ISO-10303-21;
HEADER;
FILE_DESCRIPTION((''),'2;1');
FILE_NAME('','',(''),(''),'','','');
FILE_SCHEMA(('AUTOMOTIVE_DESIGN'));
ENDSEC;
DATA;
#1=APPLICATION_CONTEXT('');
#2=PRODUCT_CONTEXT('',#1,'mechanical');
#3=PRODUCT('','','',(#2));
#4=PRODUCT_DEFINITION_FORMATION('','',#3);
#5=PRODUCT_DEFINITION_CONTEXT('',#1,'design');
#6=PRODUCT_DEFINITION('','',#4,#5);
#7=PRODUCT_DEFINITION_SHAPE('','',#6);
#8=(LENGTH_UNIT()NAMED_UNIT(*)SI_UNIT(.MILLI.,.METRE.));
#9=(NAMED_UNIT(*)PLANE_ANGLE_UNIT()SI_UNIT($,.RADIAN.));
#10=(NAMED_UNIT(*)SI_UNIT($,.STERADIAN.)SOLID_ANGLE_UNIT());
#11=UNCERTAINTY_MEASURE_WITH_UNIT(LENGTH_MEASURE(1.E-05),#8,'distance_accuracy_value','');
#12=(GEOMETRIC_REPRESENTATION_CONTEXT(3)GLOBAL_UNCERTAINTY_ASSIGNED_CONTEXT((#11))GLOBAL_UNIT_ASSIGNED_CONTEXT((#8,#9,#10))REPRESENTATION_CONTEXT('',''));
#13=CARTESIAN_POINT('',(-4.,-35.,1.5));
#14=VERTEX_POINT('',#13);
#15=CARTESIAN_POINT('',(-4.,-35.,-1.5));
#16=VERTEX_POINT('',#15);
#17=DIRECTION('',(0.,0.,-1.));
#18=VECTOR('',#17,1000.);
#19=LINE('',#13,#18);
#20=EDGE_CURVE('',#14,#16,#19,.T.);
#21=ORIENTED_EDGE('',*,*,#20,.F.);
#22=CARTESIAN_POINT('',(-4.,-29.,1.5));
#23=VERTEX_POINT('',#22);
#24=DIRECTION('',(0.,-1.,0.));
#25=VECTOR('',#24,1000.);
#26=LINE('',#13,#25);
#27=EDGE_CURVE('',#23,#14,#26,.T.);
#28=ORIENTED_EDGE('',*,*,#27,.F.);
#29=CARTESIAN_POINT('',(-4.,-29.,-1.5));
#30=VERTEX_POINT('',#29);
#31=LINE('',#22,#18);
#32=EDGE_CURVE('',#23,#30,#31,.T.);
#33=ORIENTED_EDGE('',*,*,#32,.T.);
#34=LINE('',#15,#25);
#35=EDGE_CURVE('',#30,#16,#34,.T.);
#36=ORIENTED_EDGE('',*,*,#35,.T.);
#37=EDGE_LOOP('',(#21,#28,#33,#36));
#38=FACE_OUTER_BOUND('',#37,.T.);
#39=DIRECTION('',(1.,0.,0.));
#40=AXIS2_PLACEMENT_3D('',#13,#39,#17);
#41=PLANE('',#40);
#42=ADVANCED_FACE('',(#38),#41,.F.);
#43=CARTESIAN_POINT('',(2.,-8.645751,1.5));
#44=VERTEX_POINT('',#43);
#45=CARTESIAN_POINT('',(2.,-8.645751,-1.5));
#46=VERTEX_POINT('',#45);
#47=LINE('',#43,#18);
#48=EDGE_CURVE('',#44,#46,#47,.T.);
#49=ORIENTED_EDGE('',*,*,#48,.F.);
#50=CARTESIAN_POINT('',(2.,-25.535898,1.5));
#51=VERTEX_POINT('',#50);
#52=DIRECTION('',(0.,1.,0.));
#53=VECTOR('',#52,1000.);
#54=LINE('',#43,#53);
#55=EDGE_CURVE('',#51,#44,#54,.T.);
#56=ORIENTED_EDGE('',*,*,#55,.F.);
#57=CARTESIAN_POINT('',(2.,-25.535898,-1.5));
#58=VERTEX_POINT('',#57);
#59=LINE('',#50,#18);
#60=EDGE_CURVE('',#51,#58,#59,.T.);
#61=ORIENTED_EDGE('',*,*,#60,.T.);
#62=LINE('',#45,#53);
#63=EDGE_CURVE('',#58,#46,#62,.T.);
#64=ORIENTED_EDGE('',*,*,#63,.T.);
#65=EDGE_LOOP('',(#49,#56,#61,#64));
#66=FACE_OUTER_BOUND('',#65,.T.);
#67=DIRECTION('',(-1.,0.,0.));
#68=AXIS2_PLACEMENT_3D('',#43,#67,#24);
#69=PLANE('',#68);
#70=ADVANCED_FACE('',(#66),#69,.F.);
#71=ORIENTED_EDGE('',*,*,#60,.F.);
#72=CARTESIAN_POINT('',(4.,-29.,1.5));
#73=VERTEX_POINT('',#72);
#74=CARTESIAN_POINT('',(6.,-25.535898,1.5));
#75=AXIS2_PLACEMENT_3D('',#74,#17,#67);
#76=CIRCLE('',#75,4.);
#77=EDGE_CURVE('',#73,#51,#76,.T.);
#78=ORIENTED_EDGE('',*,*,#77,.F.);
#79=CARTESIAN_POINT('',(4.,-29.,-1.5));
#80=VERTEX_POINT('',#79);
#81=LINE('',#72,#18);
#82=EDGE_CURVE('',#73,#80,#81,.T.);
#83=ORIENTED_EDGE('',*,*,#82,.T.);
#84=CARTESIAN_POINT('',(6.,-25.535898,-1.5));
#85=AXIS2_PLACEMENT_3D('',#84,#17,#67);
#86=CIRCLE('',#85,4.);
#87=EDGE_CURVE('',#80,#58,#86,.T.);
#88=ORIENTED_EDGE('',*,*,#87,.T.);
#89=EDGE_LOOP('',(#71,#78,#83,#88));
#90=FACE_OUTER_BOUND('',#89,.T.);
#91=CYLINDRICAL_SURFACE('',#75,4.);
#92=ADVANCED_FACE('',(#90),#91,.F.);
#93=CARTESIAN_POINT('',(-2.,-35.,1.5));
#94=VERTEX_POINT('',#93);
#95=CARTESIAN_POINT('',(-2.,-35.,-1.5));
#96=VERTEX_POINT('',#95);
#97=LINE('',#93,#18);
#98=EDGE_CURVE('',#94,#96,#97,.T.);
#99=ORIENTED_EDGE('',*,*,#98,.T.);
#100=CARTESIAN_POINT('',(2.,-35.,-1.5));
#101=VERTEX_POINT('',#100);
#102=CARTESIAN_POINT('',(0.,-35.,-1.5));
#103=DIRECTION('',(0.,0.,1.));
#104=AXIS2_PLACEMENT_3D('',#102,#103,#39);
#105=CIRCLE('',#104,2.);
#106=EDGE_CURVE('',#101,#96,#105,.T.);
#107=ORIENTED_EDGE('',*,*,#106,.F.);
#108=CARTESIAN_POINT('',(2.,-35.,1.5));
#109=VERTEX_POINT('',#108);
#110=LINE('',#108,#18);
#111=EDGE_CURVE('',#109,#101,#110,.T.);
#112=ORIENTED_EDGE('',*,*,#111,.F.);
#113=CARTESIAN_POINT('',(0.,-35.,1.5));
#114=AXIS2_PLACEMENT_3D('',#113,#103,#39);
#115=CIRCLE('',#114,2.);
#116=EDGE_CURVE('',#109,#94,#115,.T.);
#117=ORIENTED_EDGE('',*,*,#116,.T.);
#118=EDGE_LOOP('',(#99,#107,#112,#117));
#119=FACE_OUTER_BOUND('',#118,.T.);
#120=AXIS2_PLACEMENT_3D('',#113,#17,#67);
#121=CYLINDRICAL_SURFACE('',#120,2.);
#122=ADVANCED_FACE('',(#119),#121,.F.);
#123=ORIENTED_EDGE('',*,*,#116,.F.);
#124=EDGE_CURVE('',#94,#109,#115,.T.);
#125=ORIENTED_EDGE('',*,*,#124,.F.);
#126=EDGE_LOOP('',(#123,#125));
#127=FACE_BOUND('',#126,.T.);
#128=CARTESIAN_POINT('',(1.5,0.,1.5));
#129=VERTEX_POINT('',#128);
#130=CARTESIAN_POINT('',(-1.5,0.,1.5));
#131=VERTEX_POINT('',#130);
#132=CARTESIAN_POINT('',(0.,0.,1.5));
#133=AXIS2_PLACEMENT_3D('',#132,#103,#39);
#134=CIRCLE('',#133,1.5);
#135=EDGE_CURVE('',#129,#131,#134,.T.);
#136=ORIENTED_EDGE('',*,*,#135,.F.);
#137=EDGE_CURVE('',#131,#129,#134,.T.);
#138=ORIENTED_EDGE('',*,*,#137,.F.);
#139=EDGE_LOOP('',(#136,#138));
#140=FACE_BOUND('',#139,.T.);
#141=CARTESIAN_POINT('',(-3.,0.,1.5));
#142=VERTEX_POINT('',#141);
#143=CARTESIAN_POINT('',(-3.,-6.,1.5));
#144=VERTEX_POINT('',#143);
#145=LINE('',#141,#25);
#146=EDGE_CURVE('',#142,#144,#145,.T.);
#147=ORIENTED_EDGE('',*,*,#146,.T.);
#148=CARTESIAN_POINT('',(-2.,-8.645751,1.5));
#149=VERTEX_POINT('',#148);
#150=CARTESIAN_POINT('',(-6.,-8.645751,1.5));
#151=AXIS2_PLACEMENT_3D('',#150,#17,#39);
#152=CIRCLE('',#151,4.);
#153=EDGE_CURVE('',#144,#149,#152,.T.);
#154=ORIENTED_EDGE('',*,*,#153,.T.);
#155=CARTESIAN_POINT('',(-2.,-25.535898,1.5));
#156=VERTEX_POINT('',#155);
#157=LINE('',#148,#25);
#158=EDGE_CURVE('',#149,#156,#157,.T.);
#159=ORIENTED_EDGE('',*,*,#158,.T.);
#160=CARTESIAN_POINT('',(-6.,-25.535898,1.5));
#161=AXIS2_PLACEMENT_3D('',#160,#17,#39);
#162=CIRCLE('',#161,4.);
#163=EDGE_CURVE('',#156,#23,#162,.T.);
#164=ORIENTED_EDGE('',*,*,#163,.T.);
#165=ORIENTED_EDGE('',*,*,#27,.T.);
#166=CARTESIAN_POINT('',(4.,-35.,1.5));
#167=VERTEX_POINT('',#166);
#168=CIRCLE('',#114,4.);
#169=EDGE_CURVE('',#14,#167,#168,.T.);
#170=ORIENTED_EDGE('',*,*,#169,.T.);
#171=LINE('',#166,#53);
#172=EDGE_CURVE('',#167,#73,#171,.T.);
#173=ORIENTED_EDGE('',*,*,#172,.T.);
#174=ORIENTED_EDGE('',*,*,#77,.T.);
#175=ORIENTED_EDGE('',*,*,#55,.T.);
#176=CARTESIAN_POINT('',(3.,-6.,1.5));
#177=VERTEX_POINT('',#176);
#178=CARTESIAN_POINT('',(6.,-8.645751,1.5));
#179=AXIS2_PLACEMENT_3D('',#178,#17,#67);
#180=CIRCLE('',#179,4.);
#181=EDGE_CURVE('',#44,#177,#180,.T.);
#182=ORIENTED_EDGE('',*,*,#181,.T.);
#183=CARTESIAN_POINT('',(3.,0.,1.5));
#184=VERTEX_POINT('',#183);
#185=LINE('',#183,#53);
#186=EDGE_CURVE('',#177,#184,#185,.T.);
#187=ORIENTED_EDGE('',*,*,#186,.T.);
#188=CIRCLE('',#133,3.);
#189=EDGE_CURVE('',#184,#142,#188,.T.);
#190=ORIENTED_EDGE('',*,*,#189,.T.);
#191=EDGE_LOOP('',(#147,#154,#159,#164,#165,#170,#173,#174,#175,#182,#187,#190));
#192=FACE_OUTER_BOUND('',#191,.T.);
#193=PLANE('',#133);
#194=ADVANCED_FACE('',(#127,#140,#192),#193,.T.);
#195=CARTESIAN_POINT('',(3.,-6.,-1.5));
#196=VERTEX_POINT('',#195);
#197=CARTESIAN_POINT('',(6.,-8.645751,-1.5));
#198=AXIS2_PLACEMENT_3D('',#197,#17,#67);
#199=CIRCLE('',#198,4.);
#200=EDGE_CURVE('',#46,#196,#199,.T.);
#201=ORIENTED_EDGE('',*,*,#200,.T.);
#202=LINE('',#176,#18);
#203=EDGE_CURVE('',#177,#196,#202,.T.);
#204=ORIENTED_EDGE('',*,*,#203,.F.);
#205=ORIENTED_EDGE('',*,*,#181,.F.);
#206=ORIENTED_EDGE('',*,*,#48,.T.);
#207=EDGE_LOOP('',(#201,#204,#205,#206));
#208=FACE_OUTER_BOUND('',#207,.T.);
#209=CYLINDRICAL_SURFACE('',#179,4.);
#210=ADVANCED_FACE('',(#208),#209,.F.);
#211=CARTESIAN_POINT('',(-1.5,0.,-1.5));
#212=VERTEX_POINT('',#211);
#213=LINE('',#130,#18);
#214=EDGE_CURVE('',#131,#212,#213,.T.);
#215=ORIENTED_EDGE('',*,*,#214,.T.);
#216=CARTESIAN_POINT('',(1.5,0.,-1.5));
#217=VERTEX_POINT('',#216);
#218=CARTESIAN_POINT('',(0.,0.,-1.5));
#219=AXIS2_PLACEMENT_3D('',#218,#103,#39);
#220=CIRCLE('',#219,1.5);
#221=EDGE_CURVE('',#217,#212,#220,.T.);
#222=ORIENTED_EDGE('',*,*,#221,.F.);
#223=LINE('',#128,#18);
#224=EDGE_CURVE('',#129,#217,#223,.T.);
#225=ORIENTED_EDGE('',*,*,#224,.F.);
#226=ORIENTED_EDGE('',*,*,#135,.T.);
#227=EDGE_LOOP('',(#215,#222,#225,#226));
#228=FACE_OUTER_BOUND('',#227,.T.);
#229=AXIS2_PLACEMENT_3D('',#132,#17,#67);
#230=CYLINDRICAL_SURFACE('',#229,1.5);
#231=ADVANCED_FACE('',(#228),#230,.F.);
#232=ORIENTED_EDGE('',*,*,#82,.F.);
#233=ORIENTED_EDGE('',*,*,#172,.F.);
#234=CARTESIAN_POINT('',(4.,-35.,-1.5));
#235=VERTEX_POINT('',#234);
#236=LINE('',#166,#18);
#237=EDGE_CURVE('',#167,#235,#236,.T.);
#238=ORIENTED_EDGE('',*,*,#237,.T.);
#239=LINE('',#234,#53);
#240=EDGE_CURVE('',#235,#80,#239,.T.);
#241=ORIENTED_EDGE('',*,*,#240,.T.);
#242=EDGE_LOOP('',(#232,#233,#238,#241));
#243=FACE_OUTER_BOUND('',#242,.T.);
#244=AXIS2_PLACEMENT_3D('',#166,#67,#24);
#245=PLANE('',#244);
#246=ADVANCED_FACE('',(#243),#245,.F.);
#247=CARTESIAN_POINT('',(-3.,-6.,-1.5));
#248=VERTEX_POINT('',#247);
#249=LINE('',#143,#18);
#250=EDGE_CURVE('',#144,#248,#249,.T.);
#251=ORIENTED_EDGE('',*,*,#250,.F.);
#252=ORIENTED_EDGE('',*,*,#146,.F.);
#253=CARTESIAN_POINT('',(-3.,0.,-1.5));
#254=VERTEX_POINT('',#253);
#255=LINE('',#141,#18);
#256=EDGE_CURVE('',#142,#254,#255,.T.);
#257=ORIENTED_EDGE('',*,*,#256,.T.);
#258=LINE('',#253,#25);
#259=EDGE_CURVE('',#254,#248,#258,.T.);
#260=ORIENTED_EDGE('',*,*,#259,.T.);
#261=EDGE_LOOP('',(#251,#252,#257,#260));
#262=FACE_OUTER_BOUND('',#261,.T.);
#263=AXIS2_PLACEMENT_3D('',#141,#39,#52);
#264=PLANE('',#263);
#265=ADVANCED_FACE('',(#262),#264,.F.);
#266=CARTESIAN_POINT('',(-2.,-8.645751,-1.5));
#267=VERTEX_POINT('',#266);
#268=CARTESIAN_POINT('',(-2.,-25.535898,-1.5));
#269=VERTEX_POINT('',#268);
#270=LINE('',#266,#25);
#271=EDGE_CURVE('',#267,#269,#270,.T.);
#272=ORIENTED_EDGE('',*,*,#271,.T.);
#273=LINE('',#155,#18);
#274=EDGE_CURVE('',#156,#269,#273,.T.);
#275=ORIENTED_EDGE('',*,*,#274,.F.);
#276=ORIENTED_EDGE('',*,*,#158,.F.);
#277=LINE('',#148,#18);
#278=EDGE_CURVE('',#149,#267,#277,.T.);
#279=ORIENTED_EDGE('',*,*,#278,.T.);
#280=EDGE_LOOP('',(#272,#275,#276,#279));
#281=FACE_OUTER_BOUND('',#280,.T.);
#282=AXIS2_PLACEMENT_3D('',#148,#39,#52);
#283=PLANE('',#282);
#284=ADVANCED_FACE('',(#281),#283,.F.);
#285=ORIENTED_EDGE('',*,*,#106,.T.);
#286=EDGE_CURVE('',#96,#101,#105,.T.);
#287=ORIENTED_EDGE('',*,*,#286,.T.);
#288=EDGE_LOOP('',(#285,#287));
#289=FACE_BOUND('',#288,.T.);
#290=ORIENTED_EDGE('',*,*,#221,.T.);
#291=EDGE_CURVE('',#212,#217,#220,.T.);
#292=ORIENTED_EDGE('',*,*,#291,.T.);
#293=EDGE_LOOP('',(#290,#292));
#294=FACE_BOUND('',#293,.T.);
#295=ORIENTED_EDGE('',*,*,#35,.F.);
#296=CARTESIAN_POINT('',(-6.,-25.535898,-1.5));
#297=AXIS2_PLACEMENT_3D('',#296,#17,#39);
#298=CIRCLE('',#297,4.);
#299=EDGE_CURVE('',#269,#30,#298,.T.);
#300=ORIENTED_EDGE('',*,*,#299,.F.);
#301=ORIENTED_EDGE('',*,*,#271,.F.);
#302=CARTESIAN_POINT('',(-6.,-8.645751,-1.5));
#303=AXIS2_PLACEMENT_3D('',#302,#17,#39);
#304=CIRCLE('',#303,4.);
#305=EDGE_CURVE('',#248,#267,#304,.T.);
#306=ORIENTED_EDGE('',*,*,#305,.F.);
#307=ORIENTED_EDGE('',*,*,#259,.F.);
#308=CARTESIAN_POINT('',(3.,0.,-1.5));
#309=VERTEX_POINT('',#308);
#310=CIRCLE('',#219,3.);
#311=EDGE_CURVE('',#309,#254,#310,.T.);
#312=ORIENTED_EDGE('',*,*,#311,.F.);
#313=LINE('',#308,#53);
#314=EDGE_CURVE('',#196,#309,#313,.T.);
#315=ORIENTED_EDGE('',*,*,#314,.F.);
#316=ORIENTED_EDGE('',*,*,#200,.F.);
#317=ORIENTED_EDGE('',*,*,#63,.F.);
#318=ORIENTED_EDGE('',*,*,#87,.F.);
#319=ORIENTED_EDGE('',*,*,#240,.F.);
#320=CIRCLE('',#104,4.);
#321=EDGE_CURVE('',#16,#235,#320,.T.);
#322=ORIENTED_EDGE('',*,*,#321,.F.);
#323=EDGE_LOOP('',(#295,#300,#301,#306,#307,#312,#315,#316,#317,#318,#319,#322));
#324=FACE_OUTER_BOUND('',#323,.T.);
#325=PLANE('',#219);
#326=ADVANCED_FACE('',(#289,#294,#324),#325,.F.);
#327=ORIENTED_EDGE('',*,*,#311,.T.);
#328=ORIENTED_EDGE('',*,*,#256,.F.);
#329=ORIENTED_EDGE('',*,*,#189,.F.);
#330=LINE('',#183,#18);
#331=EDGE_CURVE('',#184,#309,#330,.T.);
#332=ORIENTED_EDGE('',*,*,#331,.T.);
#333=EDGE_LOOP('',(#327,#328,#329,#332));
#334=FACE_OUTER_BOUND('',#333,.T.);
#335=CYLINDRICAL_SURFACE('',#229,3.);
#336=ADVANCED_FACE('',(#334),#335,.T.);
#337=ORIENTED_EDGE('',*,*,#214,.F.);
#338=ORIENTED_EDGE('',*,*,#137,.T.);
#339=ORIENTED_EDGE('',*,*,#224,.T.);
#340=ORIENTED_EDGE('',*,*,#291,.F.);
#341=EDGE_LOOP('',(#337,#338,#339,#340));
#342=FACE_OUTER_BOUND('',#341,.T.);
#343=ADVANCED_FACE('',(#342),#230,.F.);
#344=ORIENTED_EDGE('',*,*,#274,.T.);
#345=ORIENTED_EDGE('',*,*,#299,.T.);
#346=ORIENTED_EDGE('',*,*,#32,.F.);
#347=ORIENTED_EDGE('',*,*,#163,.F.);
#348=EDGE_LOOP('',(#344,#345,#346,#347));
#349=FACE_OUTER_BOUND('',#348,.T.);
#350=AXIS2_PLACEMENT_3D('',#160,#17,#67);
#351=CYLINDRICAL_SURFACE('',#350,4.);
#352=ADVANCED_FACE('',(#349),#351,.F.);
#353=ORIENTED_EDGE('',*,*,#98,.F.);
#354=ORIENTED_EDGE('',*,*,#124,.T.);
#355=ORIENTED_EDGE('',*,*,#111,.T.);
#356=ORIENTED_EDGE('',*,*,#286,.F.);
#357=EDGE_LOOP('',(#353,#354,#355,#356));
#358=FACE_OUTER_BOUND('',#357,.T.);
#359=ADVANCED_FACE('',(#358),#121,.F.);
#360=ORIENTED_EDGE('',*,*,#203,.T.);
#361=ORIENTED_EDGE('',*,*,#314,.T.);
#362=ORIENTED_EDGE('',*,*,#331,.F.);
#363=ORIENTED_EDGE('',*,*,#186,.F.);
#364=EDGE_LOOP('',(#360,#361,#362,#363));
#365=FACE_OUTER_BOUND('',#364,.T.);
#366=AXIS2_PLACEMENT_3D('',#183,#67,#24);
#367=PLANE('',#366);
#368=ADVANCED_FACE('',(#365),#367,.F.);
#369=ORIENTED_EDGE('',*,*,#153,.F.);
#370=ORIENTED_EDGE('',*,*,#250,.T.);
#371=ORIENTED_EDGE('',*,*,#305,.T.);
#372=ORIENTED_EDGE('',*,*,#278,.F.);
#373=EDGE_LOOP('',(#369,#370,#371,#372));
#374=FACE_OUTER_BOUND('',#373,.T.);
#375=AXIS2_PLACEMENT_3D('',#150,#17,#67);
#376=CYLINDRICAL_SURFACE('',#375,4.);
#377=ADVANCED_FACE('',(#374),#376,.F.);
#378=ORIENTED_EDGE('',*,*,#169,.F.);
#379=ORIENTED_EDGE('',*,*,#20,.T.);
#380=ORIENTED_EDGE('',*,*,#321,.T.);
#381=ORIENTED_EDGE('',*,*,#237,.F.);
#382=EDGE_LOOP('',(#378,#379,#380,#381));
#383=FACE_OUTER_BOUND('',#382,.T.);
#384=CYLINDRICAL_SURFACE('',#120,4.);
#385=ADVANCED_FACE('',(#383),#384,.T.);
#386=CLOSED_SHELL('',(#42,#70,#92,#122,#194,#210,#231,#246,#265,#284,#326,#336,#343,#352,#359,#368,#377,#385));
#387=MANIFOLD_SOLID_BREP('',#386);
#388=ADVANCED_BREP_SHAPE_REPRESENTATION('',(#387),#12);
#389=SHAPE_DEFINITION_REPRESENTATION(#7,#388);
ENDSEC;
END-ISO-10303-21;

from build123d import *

# Parameters (mm, degrees)
SKETCH1_R           = 1.5
SKETCH1_R_2         = 2
BOSS_EXTRUDE1_DEPTH = 1.5


with BuildPart() as part:
    # Sketch1 → Boss-Extrude1 (new, symmetric)
    with BuildSketch(Plane.XY):
        with BuildLine():
            Line((-3, 0), (-3, -6))
            ThreePointArc((-3, -6), (-2.258342613, -7.231537749), (-2, -8.645751311))
            Line((-2, -8.645751311), (-2, -25.535898385))
            ThreePointArc((-2, -25.535898385), (-2.535898385, -27.535898385), (-4, -29))
            Line((-4, -29), (-4, -35))
            ThreePointArc((-4, -35), (0, -39), (4, -35))
            Line((4, -35), (4, -29))
            ThreePointArc((4, -29), (2.535898385, -27.535898385), (2, -25.535898385))
            Line((2, -25.535898385), (2, -8.645751311))
            ThreePointArc((2, -8.645751311), (2.258342613, -7.231537749), (3, -6))
            Line((3, -6), (3, 0))
            ThreePointArc((3, 0), (0, 3), (-3, 0))
        make_face()
        Circle(SKETCH1_R, mode=Mode.SUBTRACT)
        with Locations((0, -35)):
            Circle(SKETCH1_R_2, mode=Mode.SUBTRACT)
    extrude(amount=BOSS_EXTRUDE1_DEPTH, both=True)


solid = part.part
